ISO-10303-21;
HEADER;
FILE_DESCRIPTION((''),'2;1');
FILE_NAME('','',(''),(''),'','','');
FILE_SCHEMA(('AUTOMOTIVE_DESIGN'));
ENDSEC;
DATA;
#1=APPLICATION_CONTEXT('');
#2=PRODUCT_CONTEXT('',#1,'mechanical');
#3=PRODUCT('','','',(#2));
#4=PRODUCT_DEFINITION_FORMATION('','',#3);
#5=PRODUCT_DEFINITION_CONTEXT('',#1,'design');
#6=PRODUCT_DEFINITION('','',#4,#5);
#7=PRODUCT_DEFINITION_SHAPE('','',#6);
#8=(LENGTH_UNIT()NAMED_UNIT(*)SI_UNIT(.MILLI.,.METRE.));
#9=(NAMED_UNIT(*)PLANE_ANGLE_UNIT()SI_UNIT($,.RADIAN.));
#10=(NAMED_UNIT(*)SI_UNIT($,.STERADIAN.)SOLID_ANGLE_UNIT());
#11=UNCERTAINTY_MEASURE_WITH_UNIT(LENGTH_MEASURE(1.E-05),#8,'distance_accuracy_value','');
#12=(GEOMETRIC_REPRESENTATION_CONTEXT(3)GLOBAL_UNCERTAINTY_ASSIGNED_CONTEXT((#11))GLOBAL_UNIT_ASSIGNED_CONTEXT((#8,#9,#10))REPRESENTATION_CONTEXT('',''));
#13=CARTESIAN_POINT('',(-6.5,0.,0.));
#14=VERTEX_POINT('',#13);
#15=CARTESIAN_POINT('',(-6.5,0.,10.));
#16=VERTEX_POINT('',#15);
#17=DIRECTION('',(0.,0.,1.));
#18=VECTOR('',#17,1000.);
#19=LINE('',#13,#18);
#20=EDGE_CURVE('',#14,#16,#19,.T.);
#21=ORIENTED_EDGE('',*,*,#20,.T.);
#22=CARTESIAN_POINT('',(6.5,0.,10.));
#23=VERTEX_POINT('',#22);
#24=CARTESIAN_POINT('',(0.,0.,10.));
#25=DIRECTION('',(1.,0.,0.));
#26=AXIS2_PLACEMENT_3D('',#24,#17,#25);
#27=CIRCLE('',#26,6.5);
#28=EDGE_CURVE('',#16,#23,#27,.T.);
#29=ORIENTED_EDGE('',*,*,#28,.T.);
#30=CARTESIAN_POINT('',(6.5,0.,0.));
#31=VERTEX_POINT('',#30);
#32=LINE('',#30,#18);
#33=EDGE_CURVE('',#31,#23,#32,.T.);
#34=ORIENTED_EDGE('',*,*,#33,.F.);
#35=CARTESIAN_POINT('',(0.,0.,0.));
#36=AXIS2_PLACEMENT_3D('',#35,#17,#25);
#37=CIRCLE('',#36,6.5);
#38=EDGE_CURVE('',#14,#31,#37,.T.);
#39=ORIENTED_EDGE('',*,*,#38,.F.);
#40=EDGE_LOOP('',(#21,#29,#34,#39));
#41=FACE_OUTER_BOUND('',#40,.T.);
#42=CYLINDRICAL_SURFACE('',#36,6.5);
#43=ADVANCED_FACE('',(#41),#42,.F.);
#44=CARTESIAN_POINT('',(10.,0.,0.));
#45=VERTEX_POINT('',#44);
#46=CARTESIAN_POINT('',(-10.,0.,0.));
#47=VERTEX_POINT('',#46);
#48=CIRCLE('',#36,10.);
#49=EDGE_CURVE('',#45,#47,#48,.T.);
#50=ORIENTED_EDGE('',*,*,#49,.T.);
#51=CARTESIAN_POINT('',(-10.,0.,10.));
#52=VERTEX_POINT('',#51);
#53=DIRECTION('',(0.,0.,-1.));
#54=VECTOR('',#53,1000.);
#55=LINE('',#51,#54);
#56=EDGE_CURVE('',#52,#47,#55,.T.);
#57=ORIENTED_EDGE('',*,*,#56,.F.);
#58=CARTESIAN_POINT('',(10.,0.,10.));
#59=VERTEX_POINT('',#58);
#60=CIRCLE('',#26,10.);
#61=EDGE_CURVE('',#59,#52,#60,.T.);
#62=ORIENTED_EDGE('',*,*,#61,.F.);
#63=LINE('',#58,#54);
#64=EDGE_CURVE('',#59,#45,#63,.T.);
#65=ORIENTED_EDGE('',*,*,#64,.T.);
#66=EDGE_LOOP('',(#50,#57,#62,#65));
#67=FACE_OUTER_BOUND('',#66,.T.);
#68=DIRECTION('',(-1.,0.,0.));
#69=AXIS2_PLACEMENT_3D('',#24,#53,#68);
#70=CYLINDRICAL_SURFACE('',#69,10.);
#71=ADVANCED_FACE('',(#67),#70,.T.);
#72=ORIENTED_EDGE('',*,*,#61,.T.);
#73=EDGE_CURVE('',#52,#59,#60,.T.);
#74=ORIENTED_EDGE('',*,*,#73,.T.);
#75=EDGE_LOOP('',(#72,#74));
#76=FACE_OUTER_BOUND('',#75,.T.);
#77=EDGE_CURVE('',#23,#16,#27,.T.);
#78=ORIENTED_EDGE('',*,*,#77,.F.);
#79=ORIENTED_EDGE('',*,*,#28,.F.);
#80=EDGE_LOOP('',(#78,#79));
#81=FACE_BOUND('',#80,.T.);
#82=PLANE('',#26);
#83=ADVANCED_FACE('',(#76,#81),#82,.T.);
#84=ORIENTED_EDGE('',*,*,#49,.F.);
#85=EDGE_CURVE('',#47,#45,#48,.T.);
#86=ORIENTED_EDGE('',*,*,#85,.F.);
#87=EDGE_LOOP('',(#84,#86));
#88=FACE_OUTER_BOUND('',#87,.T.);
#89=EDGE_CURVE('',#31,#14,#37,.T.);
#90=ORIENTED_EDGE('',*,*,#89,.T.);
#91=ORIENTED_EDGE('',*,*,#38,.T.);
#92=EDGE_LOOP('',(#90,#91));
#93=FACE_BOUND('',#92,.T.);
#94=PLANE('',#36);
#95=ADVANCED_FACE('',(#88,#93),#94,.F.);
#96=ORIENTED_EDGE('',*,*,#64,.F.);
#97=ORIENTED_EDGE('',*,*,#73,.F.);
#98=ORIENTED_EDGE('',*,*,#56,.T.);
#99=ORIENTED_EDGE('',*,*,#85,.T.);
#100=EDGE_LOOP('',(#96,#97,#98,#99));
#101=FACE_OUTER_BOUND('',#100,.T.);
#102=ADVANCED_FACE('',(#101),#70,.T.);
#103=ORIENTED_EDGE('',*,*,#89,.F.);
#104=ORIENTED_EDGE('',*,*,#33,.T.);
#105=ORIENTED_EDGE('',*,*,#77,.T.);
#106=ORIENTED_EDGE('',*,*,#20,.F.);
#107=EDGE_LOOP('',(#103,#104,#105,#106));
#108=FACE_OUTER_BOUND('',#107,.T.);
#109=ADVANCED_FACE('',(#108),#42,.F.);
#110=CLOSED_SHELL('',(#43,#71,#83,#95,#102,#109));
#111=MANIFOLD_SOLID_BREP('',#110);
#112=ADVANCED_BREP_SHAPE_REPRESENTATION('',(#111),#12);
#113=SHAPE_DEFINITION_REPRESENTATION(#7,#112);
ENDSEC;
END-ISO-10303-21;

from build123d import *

# Parameters (mm, degrees)
SKETCH1_R          = 10
EXTRUDE1_DEPTH     = 10
SKETCH2_R          = 6.5
CUT_EXTRUDE1_DEPTH = 10


with BuildPart() as part:
    # Sketch1 → Extrude1 (new body)
    with BuildSketch(Plane.XY):
        Circle(SKETCH1_R)
    extrude(amount=EXTRUDE1_DEPTH)

    # Sketch2 → Cut-Extrude1 (cut)
    with BuildSketch(Plane.XY.offset(10)):
        Circle(SKETCH2_R)
    extrude(amount=-CUT_EXTRUDE1_DEPTH, mode=Mode.SUBTRACT)


solid = part.part
